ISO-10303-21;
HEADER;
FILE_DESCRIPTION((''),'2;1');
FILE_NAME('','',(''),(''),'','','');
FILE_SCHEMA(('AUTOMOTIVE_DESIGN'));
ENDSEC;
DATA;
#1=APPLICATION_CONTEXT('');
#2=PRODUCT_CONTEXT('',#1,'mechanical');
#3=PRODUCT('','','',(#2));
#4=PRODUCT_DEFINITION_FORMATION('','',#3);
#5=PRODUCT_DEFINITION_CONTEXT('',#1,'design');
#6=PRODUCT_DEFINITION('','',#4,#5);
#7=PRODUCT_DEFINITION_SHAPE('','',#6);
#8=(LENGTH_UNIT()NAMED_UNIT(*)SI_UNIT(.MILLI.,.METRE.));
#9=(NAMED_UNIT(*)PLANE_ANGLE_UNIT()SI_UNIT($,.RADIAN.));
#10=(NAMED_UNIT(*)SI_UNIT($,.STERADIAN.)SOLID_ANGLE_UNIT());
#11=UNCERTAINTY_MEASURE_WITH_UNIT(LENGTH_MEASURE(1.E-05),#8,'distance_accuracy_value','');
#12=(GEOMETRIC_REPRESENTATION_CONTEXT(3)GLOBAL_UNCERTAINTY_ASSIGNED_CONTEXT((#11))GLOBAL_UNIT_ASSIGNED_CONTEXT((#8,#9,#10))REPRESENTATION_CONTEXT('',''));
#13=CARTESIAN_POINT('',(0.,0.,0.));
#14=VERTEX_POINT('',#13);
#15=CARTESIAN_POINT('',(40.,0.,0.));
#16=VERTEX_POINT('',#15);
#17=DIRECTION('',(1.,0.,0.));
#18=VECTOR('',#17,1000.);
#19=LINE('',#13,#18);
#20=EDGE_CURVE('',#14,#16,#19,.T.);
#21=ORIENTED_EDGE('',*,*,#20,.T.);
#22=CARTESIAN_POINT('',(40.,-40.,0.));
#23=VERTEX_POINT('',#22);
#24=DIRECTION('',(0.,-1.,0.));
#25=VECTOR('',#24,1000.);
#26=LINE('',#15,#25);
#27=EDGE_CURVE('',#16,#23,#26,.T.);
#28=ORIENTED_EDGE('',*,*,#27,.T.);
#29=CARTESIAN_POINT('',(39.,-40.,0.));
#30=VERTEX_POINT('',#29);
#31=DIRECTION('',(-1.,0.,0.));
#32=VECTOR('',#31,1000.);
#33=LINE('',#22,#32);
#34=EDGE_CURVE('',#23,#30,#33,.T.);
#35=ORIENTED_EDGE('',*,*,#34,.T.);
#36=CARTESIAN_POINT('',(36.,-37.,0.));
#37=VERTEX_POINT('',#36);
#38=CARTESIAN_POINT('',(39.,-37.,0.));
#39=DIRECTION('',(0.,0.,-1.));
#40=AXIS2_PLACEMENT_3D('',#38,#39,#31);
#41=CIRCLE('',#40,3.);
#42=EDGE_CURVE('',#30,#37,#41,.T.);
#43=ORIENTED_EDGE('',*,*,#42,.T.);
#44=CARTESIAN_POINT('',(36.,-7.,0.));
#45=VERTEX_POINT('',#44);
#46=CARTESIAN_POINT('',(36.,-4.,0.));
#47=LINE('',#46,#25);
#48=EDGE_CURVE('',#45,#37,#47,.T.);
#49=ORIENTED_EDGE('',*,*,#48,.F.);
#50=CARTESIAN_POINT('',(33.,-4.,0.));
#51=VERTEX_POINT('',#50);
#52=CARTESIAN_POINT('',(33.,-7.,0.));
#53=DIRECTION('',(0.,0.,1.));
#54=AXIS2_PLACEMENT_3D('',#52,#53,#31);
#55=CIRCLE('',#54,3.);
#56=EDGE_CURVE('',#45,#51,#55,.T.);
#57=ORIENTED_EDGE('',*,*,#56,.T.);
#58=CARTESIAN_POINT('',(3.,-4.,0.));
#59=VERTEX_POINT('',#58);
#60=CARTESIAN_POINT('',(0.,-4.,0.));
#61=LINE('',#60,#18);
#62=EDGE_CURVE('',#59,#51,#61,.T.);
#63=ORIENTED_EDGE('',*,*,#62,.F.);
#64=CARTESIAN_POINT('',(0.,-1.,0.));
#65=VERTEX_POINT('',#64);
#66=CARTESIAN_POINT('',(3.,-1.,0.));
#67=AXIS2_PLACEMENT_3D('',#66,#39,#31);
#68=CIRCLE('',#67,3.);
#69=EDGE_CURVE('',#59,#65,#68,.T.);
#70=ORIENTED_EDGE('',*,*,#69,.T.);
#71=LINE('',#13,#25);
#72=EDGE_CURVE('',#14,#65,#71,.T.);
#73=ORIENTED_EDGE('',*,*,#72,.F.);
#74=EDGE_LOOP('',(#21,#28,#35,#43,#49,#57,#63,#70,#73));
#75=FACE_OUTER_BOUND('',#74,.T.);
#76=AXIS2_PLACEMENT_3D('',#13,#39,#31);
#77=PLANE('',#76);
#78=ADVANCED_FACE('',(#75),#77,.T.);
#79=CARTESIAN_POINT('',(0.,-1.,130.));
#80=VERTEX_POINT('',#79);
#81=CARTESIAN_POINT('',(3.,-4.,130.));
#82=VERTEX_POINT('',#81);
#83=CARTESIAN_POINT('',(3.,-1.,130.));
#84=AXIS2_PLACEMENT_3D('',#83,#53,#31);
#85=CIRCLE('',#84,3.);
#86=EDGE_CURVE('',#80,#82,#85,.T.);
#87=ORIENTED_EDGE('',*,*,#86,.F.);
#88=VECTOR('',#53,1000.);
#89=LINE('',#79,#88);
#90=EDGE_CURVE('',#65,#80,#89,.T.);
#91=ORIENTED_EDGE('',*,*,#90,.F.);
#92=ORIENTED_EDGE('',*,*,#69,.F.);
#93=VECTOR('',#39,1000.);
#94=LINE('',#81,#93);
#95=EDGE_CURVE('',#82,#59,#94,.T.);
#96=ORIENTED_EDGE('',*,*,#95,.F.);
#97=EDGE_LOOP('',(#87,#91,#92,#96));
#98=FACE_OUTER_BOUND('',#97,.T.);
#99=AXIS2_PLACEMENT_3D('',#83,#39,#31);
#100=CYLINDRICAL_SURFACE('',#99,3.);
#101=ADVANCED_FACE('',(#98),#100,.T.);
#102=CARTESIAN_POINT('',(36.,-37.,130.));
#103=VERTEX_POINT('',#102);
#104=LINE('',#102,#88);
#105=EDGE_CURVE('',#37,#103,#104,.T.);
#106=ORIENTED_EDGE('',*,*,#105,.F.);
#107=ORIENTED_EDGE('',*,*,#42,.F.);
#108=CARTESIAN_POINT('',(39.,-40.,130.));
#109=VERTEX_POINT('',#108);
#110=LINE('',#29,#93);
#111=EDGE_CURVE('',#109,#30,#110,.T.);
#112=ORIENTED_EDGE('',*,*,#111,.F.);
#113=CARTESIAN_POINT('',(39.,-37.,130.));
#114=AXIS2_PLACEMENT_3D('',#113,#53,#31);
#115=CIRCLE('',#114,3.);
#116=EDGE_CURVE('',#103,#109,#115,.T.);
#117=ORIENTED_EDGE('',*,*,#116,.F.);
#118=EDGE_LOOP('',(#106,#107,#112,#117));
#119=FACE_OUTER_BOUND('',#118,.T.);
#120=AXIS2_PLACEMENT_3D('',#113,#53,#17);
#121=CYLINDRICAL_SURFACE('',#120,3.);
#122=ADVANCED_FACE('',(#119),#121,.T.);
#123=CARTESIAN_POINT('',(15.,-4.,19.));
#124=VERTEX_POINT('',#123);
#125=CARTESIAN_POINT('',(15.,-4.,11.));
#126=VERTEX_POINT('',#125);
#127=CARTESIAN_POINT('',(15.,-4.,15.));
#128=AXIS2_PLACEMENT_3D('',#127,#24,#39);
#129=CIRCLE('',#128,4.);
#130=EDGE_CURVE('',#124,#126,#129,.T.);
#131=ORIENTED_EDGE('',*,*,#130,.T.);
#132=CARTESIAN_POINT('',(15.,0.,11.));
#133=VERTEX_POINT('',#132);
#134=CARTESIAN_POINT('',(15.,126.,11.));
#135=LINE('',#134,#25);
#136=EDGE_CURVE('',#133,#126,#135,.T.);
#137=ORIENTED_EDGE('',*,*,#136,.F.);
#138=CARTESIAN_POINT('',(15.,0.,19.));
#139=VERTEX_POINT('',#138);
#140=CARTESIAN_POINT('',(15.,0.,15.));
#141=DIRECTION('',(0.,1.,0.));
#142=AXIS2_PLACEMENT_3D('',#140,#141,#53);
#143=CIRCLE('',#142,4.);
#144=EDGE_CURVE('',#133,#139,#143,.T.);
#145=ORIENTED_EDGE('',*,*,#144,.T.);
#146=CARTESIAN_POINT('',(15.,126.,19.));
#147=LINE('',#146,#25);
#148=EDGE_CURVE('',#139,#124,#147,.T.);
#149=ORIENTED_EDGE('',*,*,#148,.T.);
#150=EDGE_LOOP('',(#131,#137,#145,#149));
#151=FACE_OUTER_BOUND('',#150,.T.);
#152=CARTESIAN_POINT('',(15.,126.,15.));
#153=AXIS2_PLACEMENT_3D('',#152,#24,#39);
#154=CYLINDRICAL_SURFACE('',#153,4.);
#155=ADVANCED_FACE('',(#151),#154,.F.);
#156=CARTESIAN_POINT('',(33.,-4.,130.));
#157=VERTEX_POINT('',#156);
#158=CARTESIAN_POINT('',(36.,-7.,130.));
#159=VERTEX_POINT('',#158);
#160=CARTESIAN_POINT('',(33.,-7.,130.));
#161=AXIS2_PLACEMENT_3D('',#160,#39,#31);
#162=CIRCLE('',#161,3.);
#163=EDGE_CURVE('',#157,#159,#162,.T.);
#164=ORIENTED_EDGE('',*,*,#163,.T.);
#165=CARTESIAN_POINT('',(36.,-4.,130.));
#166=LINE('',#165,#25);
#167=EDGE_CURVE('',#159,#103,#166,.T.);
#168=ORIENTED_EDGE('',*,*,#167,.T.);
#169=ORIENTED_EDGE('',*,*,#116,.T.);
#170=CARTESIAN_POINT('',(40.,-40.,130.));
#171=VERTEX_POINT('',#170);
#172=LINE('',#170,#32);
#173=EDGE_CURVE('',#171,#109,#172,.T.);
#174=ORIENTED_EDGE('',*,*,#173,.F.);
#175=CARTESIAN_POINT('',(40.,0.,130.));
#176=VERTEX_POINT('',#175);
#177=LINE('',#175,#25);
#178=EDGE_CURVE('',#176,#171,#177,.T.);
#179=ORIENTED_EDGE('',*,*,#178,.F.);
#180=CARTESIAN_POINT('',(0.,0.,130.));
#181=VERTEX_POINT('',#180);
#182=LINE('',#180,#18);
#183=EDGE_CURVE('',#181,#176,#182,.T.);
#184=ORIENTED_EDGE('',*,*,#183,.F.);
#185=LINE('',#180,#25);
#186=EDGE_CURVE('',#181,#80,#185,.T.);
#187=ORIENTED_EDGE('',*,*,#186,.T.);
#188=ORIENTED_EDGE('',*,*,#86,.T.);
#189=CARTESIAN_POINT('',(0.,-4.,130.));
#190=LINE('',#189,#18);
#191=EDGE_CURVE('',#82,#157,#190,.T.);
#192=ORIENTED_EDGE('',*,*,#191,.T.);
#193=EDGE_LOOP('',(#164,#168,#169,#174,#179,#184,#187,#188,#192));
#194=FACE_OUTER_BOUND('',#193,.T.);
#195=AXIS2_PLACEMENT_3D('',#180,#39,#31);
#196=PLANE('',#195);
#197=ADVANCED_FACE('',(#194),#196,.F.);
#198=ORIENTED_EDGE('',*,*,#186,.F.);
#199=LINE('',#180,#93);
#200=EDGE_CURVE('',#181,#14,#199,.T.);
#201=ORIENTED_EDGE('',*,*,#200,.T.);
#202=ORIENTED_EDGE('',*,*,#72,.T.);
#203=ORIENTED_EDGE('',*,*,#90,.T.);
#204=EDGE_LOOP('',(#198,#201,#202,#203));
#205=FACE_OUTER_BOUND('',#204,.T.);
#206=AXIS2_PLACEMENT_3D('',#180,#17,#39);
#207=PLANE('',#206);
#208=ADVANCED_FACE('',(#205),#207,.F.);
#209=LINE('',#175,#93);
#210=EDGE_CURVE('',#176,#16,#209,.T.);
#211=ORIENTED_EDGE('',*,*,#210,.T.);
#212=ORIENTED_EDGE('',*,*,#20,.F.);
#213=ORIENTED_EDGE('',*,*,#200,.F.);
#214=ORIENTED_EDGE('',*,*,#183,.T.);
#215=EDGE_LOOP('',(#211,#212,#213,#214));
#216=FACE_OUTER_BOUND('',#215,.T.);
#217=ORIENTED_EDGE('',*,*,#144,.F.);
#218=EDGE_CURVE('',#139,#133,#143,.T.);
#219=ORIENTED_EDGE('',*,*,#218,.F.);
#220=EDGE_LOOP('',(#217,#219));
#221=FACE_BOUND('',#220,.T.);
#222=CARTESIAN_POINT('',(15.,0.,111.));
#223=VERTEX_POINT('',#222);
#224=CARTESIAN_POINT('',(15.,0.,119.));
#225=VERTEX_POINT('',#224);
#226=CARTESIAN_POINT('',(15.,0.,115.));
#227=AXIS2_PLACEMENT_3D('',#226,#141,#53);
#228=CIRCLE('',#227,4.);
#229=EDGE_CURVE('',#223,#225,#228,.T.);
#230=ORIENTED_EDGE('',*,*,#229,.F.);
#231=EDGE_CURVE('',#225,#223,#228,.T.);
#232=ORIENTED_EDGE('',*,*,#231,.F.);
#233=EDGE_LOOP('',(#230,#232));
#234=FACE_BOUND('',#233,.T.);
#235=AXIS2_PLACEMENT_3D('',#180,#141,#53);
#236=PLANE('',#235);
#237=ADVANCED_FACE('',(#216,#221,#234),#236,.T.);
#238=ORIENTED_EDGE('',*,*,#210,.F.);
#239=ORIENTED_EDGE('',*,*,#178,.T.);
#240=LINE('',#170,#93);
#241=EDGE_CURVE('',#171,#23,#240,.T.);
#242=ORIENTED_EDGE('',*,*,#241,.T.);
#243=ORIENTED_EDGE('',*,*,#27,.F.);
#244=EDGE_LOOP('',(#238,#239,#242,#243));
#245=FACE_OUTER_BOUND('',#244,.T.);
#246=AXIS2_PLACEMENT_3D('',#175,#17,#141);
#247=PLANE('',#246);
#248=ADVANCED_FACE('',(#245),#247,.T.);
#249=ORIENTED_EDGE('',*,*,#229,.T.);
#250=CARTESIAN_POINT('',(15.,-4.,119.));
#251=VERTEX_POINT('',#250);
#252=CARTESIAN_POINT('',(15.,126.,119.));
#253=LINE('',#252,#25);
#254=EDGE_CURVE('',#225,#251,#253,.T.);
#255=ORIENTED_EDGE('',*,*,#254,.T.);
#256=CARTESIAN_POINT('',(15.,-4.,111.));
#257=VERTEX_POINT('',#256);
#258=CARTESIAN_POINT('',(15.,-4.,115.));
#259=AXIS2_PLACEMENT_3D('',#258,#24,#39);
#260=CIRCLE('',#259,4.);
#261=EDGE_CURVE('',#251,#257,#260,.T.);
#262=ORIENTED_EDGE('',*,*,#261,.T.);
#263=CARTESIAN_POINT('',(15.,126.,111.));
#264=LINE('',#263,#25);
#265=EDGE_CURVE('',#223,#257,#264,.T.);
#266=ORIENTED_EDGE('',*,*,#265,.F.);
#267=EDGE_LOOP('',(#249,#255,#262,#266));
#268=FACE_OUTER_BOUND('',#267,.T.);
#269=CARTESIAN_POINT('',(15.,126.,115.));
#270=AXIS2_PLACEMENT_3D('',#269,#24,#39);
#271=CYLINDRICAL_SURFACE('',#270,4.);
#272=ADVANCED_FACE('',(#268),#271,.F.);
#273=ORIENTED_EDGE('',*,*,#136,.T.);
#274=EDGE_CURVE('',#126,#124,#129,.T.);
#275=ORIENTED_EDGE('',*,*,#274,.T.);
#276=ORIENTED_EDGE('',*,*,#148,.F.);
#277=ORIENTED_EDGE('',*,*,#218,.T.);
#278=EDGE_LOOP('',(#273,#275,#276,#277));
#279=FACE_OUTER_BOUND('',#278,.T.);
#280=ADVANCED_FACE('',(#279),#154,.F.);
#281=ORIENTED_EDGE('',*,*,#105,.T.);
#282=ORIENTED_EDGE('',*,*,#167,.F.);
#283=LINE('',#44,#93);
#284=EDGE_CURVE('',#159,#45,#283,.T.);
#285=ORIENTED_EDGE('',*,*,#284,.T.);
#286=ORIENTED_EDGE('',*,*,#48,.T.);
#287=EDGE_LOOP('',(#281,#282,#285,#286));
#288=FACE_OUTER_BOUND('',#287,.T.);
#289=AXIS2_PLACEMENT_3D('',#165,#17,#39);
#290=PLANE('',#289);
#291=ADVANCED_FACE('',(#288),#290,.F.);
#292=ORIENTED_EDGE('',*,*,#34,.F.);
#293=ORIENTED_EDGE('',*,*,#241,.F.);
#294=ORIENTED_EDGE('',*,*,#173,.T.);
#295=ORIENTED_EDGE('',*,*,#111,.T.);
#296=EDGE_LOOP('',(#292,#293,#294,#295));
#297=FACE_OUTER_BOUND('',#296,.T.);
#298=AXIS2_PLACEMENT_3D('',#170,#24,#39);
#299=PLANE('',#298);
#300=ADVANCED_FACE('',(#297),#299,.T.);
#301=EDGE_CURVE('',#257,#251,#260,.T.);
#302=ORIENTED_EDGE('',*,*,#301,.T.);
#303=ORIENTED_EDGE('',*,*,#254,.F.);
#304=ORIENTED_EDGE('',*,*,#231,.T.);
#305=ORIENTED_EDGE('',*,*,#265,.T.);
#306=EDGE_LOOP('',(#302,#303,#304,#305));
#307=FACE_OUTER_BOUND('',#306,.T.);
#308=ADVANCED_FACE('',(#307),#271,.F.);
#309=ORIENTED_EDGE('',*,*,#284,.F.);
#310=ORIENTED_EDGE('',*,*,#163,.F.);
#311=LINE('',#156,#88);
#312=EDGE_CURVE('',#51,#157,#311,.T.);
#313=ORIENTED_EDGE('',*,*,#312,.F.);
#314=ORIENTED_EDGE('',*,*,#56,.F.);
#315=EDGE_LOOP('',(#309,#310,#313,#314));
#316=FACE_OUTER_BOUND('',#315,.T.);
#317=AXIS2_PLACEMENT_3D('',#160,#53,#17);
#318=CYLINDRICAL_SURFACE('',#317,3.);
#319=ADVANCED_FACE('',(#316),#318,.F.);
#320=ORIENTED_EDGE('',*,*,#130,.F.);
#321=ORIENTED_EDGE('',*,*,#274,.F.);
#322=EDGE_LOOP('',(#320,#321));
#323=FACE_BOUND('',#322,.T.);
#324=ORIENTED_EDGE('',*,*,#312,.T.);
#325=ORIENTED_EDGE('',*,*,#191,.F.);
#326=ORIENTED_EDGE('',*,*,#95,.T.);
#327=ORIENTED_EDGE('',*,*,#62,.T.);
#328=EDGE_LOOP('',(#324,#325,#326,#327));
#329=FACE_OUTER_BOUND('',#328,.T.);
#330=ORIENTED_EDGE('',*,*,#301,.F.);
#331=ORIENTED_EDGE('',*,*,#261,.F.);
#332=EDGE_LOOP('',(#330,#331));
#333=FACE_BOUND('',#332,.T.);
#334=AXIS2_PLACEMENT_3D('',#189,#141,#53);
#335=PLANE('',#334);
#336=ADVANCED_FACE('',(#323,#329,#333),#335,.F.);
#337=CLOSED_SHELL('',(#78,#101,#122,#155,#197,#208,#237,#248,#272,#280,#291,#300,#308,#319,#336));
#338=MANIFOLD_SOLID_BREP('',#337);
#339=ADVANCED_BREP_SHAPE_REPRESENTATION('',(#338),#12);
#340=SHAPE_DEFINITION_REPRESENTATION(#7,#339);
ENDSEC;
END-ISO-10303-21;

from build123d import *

# Parameters (mm, degrees)
BOSS_EXTRUDE1_DEPTH = 130
FILLET1_R           = 3
SKETCH2_R           = 4
CUT_EXTRUDE1_DEPTH  = 130


with BuildPart() as part:
    # Sketch1 → Boss-Extrude1 (new body)
    with BuildSketch(Plane.XY):
        Polygon((0, 0), (40, 0), (40, -40), (36, -40), (36, -4), (0, -4), align=None)
    extrude(amount=BOSS_EXTRUDE1_DEPTH)

    # Fillet1
    fillet1_edges = [part.edges().sort_by_distance(p)[0] for p in [
        (0, -4, 65),
        (36, -4, 65),
        (36, -40, 65),
    ]]
    fillet(fillet1_edges, radius=FILLET1_R)

    # Sketch2 → Cut-Extrude1 (cut)
    with BuildSketch(Plane.XZ.offset(4)):
        with Locations(Location((15, 115, 0), (0, 0, 270))):
            Circle(SKETCH2_R)
        with Locations(Location((15, 15, 0), (0, 0, 270))):
            Circle(SKETCH2_R)
    extrude(amount=-CUT_EXTRUDE1_DEPTH, mode=Mode.SUBTRACT)


solid = part.part
